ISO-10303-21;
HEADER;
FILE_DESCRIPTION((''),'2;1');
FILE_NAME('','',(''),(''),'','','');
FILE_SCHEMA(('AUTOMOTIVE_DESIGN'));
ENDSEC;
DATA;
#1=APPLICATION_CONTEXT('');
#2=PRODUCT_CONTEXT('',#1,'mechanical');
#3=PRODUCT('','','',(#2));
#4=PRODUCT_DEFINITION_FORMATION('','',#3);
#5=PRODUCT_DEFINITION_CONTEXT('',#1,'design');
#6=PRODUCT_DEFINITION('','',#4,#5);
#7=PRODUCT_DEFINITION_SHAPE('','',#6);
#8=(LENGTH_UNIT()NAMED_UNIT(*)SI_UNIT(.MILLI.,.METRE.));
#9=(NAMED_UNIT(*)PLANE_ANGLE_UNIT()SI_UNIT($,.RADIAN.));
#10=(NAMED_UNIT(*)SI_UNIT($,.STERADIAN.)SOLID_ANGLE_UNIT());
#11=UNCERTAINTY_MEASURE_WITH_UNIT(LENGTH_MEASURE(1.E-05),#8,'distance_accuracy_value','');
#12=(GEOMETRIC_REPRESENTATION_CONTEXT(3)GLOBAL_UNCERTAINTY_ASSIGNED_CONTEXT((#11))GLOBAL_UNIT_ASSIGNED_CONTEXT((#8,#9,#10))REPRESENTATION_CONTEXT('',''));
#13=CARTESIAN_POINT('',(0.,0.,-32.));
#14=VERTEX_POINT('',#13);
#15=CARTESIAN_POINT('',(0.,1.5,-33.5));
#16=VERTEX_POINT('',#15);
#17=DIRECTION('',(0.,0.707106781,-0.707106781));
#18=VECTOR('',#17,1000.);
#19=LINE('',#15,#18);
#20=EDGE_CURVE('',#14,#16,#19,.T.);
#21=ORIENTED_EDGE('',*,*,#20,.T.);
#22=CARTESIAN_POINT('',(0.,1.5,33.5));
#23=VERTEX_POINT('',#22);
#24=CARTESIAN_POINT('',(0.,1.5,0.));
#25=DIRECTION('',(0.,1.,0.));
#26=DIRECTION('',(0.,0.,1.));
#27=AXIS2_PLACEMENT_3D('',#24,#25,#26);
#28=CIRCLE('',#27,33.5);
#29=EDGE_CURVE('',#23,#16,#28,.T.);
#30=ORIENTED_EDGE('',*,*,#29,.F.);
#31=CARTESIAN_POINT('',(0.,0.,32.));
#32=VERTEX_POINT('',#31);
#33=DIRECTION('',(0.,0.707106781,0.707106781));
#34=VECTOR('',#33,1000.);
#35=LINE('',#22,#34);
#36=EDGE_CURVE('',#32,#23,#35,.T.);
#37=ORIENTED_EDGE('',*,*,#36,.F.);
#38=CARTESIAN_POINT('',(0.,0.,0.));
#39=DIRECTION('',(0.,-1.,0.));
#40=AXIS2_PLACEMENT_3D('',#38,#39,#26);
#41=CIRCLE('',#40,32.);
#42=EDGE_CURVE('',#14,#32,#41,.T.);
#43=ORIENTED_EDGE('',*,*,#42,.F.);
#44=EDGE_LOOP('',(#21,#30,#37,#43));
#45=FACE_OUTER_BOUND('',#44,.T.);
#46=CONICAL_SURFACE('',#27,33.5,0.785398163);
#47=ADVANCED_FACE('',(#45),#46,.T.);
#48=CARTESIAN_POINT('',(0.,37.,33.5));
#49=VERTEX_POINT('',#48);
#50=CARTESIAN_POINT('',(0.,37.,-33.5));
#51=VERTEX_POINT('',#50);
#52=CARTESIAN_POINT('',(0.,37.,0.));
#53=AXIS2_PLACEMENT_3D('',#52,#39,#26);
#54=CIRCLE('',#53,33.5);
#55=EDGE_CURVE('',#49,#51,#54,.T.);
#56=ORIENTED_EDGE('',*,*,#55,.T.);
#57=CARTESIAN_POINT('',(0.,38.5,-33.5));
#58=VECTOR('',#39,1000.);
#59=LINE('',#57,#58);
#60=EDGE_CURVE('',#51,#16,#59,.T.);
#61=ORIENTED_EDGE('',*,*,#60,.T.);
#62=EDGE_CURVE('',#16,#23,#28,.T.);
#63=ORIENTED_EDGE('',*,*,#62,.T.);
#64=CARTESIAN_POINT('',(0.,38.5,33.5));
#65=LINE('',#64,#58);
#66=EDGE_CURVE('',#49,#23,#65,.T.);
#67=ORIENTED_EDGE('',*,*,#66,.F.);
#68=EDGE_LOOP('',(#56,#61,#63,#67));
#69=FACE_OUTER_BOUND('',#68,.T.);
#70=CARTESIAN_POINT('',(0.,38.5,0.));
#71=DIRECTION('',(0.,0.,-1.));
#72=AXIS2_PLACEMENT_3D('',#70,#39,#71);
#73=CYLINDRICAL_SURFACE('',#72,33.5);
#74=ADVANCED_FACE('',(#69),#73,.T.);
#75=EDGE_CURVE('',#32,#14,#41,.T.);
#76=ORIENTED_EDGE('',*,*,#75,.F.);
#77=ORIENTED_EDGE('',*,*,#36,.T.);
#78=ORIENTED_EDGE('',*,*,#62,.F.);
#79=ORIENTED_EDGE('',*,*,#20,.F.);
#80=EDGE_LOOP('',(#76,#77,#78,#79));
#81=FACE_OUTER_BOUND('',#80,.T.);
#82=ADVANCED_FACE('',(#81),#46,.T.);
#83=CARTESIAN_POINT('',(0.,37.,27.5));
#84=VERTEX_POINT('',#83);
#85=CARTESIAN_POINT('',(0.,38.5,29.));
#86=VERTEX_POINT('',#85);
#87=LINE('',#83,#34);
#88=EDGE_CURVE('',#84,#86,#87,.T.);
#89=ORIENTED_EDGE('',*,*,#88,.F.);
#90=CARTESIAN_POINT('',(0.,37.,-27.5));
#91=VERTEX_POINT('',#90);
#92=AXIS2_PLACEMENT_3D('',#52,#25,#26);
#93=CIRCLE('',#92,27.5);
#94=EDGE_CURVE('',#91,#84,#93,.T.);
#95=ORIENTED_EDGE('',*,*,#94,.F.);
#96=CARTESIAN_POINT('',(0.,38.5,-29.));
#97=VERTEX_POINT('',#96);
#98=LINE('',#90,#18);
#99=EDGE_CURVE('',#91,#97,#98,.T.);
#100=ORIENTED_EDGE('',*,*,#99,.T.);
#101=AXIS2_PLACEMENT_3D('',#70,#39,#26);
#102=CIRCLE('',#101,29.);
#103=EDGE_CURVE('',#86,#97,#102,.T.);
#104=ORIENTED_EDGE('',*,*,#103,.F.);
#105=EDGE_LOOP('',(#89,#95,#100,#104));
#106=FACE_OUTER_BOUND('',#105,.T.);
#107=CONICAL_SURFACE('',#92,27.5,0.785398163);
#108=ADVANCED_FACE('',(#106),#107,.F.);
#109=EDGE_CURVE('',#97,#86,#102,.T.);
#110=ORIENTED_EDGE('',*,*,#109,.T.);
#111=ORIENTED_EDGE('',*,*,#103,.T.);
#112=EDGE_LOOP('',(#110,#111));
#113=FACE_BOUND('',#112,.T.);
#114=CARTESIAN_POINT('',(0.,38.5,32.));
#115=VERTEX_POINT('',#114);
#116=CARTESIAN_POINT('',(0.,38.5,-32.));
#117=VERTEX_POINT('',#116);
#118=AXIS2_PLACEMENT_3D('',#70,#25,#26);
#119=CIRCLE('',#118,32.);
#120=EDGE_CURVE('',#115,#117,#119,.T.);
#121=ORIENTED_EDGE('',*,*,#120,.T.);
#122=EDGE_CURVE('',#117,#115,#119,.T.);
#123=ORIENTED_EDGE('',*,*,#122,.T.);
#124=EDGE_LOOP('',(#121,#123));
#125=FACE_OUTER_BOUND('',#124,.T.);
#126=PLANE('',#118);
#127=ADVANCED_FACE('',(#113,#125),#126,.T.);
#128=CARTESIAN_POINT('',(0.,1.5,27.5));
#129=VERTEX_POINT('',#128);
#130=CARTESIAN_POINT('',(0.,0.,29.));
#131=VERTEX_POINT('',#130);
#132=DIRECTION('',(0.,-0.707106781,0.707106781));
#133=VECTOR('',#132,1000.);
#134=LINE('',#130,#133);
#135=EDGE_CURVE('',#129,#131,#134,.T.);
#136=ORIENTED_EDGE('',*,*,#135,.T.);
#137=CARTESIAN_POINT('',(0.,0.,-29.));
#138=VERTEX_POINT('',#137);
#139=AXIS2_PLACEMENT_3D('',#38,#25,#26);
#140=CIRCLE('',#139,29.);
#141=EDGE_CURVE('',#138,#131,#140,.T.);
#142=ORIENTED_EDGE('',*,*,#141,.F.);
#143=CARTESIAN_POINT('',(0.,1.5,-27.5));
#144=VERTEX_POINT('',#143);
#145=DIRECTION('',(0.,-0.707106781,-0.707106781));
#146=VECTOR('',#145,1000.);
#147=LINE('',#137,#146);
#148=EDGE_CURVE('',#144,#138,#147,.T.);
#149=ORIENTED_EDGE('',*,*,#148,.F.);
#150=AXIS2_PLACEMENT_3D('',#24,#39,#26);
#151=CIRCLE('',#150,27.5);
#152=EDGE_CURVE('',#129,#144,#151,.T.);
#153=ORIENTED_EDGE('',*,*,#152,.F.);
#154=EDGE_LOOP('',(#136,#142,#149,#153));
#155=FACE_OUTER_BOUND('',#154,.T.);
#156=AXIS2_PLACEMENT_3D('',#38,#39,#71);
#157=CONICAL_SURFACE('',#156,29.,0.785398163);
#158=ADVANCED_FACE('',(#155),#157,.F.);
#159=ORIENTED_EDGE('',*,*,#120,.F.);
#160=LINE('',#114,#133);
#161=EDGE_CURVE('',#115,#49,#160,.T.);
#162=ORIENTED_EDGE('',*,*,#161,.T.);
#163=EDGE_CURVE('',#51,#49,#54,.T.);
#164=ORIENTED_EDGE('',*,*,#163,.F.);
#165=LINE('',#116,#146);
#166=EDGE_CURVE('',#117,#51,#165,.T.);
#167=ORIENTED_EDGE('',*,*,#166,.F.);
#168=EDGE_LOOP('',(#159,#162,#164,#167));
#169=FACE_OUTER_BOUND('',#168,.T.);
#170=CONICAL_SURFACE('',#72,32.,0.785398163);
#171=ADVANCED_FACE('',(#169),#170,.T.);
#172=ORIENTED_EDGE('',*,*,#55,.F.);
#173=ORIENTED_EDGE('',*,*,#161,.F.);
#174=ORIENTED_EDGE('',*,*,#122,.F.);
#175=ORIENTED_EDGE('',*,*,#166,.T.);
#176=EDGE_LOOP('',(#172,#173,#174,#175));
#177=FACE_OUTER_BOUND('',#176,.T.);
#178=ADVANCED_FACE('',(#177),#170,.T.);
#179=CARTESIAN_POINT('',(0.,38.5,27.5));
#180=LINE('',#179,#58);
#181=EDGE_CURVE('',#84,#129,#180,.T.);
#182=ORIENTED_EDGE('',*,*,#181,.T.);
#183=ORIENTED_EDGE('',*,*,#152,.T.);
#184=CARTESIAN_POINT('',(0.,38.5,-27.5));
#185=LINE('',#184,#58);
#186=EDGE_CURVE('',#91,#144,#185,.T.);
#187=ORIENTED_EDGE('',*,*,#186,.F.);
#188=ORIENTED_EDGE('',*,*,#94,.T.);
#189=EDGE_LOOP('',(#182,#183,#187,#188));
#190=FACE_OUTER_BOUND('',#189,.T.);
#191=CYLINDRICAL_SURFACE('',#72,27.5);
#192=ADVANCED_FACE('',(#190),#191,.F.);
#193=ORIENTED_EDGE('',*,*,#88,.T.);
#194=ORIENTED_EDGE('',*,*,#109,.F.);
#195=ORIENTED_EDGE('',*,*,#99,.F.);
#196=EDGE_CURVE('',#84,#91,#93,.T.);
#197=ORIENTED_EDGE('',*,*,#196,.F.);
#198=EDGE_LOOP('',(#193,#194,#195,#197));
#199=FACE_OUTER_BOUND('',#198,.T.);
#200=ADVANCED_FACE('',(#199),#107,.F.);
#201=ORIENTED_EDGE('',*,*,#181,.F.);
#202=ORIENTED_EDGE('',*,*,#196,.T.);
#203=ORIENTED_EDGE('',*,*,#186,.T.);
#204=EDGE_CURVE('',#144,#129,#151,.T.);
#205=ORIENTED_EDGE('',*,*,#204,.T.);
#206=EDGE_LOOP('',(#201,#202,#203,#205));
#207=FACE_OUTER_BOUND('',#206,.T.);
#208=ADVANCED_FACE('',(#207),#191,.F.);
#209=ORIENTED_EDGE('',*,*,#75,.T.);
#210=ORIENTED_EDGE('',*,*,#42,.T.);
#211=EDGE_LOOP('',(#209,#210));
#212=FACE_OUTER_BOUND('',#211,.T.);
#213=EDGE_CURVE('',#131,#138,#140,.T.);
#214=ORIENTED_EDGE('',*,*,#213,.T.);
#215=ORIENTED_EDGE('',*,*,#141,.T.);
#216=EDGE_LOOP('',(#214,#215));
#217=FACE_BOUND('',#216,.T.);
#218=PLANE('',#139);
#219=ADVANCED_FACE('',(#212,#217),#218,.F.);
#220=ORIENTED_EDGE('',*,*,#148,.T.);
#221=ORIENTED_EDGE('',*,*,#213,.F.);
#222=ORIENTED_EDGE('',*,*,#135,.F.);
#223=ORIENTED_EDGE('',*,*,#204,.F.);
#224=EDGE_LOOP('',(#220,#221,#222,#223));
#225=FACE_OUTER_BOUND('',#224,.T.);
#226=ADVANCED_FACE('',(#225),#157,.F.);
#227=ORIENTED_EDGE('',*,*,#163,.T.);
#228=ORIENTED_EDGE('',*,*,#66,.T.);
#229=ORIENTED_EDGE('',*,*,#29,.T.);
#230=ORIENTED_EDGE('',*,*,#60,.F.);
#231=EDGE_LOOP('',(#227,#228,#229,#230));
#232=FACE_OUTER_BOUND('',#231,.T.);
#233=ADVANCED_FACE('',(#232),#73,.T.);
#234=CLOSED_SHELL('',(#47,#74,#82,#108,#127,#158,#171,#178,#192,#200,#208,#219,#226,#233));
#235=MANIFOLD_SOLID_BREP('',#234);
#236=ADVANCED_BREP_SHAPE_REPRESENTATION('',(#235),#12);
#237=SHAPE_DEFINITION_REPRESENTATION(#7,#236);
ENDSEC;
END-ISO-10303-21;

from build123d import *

# Parameters (mm, degrees)
SKETCH1_R           = 33.5
SKETCH1_R_2         = 27.5
BOSS_EXTRUDE1_DEPTH = 38.5
CHAMFER1_SIZE       = 1.5


with BuildPart() as part:
    # Sketch1 → Boss-Extrude1 (new body)
    with BuildSketch(Plane(origin=(0, 0, 0), x_dir=(1, 0, 0), z_dir=(0, 1, 0))):
        with Locations(Location((0, 0, 0), (0, 0, 270))):
            Circle(SKETCH1_R)
        with Locations(Location((0, 0, 0), (0, 0, 270))):
            Circle(SKETCH1_R_2, mode=Mode.SUBTRACT)
    extrude(amount=BOSS_EXTRUDE1_DEPTH)

    # Chamfer1
    chamfer1_edges = [part.edges().sort_by_distance(p)[0] for p in [
        (0, 0, -33.5),
        (0, 38.5, -33.5),
        (0, 0, -27.5),
        (0, 38.5, -27.5),
    ]]
    chamfer(chamfer1_edges, length=CHAMFER1_SIZE)


solid = part.part
